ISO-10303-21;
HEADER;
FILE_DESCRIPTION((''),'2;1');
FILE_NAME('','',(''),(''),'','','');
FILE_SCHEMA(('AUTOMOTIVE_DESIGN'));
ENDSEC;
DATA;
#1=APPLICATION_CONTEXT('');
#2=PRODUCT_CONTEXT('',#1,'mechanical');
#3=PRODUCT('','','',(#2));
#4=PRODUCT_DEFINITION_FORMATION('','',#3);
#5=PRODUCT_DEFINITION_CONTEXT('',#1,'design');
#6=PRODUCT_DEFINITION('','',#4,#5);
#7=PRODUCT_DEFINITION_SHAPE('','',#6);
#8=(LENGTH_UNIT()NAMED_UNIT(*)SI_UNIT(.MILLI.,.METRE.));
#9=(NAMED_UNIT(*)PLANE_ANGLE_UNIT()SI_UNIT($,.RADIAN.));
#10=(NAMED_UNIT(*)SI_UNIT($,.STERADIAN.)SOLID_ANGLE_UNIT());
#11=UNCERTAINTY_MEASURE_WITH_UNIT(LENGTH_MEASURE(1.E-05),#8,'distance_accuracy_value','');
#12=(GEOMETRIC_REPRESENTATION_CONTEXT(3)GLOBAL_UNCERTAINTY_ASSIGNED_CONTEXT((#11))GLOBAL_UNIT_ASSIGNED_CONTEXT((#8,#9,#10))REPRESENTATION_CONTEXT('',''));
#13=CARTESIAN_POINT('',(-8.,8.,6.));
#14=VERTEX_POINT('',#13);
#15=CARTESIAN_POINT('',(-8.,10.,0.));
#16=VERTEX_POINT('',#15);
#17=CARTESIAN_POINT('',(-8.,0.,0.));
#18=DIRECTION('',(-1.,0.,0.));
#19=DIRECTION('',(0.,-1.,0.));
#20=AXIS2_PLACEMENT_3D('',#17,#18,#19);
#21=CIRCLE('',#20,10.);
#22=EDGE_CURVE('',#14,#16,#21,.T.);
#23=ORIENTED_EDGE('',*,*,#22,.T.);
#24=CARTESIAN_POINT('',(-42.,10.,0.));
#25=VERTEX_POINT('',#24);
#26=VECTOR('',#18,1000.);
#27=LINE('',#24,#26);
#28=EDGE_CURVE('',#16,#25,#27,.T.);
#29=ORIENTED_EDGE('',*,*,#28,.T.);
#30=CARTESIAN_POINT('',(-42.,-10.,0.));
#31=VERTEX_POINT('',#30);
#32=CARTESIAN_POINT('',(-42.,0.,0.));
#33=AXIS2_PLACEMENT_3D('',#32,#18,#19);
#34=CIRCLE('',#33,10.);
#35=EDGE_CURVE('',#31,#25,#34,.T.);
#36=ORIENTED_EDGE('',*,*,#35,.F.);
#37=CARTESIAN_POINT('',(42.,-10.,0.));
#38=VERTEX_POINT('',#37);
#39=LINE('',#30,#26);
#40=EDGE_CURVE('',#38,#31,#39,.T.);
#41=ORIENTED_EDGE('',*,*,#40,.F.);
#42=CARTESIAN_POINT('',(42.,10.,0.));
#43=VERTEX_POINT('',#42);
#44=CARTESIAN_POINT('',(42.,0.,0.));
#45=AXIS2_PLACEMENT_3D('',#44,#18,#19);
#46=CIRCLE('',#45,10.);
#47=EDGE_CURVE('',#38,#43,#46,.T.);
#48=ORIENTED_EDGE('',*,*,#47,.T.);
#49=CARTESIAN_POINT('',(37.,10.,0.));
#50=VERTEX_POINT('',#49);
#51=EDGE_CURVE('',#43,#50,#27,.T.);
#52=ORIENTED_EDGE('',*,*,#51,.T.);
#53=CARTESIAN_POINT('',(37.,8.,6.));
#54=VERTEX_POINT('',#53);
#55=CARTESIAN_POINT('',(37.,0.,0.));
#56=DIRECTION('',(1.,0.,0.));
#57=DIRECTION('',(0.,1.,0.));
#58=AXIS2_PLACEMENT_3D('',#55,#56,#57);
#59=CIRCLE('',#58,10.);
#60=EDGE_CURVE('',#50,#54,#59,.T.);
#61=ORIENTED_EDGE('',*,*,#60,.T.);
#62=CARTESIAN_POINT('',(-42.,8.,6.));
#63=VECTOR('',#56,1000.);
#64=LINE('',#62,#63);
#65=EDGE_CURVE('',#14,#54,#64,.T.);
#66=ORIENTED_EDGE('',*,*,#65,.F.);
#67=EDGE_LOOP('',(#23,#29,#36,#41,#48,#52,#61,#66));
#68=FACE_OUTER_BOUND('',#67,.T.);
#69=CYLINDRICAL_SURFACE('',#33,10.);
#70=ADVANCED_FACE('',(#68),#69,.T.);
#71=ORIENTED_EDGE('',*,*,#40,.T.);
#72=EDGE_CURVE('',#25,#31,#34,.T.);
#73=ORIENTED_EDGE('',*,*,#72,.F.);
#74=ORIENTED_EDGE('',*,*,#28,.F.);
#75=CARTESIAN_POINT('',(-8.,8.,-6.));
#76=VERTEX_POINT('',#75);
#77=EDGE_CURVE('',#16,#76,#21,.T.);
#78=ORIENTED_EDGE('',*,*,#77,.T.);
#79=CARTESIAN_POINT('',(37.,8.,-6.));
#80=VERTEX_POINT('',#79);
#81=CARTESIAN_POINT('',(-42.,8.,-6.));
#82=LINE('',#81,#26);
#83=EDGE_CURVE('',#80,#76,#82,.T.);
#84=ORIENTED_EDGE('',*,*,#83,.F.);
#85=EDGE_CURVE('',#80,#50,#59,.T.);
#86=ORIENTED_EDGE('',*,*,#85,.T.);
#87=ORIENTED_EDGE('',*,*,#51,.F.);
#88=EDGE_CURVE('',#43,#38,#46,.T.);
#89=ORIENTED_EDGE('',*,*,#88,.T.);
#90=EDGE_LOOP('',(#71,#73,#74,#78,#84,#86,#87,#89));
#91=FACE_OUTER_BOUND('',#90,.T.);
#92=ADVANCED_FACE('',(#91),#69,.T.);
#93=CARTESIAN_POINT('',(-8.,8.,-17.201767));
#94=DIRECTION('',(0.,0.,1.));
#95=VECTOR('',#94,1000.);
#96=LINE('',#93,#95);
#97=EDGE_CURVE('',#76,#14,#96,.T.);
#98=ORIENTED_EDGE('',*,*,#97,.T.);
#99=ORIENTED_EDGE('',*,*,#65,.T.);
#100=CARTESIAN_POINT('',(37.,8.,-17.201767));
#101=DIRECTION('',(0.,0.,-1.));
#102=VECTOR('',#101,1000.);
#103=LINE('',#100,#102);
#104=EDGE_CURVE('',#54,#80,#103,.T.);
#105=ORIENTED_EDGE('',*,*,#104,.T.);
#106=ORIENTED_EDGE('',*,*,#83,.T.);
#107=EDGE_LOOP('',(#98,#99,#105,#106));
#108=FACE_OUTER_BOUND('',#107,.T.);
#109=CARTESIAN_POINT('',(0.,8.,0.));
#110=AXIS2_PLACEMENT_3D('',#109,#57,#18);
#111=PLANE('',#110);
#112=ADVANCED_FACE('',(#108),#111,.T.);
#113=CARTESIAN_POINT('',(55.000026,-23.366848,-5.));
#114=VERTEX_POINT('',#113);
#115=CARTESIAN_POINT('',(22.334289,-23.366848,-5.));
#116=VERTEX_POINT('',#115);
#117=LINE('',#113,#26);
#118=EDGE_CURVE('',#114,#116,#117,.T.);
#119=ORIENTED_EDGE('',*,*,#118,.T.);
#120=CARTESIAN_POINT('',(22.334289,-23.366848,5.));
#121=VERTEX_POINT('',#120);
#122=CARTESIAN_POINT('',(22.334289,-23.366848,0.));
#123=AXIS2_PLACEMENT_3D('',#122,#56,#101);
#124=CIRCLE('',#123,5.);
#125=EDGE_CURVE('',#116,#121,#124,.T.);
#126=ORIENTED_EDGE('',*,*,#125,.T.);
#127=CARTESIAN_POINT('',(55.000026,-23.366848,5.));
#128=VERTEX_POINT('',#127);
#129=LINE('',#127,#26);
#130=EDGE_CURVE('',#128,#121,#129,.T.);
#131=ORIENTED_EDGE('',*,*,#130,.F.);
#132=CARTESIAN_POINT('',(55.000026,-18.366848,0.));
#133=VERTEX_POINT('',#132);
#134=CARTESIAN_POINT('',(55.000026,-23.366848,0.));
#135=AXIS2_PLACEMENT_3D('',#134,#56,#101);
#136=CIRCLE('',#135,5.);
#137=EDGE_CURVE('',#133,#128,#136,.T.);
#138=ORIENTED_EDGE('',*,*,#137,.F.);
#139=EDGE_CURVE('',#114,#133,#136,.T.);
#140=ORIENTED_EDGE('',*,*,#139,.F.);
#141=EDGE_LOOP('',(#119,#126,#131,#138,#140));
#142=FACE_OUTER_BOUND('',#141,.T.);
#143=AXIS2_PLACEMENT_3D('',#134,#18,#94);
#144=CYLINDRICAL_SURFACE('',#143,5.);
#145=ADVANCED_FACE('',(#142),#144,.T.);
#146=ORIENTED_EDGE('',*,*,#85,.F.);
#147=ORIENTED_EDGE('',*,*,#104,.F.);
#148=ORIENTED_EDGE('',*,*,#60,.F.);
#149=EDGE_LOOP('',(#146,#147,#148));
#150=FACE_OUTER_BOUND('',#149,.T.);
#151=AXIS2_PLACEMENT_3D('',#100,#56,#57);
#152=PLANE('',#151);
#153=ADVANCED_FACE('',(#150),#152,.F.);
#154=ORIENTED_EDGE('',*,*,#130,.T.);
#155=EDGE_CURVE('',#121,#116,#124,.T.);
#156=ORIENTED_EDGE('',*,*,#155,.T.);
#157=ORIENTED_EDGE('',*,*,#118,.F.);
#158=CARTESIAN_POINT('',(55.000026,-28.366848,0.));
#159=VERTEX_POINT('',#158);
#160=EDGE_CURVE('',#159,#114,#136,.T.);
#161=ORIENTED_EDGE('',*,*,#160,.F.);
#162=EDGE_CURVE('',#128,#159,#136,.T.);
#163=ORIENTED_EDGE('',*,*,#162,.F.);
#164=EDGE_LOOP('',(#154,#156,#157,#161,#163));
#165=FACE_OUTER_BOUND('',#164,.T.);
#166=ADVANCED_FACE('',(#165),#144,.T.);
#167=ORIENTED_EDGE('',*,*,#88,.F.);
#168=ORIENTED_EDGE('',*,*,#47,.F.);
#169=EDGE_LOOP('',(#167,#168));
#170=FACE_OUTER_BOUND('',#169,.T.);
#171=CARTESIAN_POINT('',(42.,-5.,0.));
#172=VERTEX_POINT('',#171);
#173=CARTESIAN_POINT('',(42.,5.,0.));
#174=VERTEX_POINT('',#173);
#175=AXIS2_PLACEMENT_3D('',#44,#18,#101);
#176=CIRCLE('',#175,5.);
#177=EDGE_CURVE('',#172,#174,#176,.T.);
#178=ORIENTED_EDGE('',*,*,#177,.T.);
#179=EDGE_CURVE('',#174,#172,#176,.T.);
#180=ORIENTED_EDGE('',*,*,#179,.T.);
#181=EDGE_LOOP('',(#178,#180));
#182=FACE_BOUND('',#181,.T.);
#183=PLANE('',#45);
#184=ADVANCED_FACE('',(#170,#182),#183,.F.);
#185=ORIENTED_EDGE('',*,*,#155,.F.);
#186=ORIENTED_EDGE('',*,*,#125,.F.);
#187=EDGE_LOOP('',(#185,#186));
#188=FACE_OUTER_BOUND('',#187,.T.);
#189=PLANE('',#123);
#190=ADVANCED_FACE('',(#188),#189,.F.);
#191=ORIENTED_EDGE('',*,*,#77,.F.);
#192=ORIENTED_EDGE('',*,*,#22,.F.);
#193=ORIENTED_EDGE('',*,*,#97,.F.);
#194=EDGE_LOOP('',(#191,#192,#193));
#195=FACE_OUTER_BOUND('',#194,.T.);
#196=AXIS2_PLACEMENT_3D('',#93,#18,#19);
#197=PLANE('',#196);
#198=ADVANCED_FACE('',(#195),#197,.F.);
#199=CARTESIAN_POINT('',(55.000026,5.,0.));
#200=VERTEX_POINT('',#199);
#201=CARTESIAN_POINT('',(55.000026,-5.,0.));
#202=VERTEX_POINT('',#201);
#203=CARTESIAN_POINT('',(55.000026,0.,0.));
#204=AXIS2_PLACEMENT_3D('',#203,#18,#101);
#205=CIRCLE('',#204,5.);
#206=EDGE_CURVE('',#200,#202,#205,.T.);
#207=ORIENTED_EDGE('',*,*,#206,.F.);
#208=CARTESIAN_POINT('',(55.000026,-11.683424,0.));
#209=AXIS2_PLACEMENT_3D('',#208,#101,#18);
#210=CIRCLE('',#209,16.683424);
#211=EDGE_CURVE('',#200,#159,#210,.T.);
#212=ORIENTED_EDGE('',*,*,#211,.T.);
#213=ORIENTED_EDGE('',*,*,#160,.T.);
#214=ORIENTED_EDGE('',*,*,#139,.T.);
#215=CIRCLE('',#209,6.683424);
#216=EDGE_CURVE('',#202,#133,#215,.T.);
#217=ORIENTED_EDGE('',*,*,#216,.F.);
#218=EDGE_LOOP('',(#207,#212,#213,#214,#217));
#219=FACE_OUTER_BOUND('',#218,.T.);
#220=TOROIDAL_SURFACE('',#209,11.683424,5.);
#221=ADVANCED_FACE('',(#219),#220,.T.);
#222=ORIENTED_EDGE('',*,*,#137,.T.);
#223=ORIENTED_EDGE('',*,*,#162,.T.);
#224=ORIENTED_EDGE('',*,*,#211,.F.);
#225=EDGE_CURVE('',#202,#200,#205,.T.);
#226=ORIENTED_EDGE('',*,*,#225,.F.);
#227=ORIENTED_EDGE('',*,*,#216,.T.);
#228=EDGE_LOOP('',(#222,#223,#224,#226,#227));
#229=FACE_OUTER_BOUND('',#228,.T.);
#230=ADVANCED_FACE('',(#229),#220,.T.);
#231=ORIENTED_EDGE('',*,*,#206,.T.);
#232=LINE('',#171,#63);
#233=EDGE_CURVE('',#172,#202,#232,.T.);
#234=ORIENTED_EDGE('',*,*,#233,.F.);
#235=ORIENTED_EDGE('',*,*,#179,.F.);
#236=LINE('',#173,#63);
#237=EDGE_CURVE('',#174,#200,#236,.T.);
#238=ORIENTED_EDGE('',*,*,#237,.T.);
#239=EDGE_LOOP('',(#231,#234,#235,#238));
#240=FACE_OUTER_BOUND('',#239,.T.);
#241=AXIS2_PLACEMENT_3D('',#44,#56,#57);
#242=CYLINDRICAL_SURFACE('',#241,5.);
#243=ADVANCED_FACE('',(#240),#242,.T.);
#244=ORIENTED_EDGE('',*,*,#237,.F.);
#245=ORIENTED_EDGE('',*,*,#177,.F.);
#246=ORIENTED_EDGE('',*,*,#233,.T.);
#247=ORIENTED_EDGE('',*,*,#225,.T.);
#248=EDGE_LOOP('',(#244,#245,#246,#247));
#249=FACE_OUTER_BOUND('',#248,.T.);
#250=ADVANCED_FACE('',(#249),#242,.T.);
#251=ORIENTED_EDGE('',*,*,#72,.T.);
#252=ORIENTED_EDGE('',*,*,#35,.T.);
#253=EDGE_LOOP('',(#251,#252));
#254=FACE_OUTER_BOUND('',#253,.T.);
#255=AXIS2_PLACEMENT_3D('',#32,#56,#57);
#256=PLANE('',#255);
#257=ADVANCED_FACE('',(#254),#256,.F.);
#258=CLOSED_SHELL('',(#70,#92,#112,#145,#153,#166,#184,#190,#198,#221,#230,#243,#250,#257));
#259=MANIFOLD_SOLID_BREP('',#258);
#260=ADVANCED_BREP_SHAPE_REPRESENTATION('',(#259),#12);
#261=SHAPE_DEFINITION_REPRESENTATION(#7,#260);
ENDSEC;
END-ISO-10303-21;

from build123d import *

# Parameters (mm, degrees)
SKETCH_1_W          = 84
SKETCH_1_H          = 10
SKETCH_2_W          = 45
SKETCH_2_H          = 40.446231626
CUT_EXTRUDE_1_DEPTH = 2
SWEEP_1_PROFILE_R   = 5


with BuildPart() as part:
    # 草图1 → 旋转1 (revolve)
    with BuildSketch(Plane.XY, mode=Mode.PRIVATE) as revolve_1_sk:
        with Locations((0, 5)):
            Rectangle(SKETCH_1_W, SKETCH_1_H)
    revolve(revolve_1_sk.sketch.rotate(Axis((-42, 0, 0), (1, 0, 0)), 180), axis=Axis((-42, 0, 0), (1, 0, 0)))

    # 草图2 → 切除-拉伸1 (cut)
    with BuildSketch(Plane(origin=(0, 10, 0), x_dir=(1, 0, 0), z_dir=(0, 1, 0))):
        with Locations((14.5, -3.02134906)):
            Rectangle(SKETCH_2_W, SKETCH_2_H)
    extrude(amount=-CUT_EXTRUDE_1_DEPTH, mode=Mode.SUBTRACT)

    # 扫描1: sweep along a path in 草图3
    with BuildLine(Plane.XY) as sweep_1_path:
        Line((42, 0), (55.00002565, 0))
        ThreePointArc((55.00002565, 0), (66.683449814, -11.683424164), (55.00002565, -23.366848328))
        Line((55.00002565, -23.366848328), (22.334289366, -23.366848328))
    # 扫描1 profile (on start of the path) → 扫描1 (sweep)
    with BuildSketch(Plane.YZ.offset(42)):
        Circle(SWEEP_1_PROFILE_R)
    sweep(path=sweep_1_path.line)


solid = part.part
